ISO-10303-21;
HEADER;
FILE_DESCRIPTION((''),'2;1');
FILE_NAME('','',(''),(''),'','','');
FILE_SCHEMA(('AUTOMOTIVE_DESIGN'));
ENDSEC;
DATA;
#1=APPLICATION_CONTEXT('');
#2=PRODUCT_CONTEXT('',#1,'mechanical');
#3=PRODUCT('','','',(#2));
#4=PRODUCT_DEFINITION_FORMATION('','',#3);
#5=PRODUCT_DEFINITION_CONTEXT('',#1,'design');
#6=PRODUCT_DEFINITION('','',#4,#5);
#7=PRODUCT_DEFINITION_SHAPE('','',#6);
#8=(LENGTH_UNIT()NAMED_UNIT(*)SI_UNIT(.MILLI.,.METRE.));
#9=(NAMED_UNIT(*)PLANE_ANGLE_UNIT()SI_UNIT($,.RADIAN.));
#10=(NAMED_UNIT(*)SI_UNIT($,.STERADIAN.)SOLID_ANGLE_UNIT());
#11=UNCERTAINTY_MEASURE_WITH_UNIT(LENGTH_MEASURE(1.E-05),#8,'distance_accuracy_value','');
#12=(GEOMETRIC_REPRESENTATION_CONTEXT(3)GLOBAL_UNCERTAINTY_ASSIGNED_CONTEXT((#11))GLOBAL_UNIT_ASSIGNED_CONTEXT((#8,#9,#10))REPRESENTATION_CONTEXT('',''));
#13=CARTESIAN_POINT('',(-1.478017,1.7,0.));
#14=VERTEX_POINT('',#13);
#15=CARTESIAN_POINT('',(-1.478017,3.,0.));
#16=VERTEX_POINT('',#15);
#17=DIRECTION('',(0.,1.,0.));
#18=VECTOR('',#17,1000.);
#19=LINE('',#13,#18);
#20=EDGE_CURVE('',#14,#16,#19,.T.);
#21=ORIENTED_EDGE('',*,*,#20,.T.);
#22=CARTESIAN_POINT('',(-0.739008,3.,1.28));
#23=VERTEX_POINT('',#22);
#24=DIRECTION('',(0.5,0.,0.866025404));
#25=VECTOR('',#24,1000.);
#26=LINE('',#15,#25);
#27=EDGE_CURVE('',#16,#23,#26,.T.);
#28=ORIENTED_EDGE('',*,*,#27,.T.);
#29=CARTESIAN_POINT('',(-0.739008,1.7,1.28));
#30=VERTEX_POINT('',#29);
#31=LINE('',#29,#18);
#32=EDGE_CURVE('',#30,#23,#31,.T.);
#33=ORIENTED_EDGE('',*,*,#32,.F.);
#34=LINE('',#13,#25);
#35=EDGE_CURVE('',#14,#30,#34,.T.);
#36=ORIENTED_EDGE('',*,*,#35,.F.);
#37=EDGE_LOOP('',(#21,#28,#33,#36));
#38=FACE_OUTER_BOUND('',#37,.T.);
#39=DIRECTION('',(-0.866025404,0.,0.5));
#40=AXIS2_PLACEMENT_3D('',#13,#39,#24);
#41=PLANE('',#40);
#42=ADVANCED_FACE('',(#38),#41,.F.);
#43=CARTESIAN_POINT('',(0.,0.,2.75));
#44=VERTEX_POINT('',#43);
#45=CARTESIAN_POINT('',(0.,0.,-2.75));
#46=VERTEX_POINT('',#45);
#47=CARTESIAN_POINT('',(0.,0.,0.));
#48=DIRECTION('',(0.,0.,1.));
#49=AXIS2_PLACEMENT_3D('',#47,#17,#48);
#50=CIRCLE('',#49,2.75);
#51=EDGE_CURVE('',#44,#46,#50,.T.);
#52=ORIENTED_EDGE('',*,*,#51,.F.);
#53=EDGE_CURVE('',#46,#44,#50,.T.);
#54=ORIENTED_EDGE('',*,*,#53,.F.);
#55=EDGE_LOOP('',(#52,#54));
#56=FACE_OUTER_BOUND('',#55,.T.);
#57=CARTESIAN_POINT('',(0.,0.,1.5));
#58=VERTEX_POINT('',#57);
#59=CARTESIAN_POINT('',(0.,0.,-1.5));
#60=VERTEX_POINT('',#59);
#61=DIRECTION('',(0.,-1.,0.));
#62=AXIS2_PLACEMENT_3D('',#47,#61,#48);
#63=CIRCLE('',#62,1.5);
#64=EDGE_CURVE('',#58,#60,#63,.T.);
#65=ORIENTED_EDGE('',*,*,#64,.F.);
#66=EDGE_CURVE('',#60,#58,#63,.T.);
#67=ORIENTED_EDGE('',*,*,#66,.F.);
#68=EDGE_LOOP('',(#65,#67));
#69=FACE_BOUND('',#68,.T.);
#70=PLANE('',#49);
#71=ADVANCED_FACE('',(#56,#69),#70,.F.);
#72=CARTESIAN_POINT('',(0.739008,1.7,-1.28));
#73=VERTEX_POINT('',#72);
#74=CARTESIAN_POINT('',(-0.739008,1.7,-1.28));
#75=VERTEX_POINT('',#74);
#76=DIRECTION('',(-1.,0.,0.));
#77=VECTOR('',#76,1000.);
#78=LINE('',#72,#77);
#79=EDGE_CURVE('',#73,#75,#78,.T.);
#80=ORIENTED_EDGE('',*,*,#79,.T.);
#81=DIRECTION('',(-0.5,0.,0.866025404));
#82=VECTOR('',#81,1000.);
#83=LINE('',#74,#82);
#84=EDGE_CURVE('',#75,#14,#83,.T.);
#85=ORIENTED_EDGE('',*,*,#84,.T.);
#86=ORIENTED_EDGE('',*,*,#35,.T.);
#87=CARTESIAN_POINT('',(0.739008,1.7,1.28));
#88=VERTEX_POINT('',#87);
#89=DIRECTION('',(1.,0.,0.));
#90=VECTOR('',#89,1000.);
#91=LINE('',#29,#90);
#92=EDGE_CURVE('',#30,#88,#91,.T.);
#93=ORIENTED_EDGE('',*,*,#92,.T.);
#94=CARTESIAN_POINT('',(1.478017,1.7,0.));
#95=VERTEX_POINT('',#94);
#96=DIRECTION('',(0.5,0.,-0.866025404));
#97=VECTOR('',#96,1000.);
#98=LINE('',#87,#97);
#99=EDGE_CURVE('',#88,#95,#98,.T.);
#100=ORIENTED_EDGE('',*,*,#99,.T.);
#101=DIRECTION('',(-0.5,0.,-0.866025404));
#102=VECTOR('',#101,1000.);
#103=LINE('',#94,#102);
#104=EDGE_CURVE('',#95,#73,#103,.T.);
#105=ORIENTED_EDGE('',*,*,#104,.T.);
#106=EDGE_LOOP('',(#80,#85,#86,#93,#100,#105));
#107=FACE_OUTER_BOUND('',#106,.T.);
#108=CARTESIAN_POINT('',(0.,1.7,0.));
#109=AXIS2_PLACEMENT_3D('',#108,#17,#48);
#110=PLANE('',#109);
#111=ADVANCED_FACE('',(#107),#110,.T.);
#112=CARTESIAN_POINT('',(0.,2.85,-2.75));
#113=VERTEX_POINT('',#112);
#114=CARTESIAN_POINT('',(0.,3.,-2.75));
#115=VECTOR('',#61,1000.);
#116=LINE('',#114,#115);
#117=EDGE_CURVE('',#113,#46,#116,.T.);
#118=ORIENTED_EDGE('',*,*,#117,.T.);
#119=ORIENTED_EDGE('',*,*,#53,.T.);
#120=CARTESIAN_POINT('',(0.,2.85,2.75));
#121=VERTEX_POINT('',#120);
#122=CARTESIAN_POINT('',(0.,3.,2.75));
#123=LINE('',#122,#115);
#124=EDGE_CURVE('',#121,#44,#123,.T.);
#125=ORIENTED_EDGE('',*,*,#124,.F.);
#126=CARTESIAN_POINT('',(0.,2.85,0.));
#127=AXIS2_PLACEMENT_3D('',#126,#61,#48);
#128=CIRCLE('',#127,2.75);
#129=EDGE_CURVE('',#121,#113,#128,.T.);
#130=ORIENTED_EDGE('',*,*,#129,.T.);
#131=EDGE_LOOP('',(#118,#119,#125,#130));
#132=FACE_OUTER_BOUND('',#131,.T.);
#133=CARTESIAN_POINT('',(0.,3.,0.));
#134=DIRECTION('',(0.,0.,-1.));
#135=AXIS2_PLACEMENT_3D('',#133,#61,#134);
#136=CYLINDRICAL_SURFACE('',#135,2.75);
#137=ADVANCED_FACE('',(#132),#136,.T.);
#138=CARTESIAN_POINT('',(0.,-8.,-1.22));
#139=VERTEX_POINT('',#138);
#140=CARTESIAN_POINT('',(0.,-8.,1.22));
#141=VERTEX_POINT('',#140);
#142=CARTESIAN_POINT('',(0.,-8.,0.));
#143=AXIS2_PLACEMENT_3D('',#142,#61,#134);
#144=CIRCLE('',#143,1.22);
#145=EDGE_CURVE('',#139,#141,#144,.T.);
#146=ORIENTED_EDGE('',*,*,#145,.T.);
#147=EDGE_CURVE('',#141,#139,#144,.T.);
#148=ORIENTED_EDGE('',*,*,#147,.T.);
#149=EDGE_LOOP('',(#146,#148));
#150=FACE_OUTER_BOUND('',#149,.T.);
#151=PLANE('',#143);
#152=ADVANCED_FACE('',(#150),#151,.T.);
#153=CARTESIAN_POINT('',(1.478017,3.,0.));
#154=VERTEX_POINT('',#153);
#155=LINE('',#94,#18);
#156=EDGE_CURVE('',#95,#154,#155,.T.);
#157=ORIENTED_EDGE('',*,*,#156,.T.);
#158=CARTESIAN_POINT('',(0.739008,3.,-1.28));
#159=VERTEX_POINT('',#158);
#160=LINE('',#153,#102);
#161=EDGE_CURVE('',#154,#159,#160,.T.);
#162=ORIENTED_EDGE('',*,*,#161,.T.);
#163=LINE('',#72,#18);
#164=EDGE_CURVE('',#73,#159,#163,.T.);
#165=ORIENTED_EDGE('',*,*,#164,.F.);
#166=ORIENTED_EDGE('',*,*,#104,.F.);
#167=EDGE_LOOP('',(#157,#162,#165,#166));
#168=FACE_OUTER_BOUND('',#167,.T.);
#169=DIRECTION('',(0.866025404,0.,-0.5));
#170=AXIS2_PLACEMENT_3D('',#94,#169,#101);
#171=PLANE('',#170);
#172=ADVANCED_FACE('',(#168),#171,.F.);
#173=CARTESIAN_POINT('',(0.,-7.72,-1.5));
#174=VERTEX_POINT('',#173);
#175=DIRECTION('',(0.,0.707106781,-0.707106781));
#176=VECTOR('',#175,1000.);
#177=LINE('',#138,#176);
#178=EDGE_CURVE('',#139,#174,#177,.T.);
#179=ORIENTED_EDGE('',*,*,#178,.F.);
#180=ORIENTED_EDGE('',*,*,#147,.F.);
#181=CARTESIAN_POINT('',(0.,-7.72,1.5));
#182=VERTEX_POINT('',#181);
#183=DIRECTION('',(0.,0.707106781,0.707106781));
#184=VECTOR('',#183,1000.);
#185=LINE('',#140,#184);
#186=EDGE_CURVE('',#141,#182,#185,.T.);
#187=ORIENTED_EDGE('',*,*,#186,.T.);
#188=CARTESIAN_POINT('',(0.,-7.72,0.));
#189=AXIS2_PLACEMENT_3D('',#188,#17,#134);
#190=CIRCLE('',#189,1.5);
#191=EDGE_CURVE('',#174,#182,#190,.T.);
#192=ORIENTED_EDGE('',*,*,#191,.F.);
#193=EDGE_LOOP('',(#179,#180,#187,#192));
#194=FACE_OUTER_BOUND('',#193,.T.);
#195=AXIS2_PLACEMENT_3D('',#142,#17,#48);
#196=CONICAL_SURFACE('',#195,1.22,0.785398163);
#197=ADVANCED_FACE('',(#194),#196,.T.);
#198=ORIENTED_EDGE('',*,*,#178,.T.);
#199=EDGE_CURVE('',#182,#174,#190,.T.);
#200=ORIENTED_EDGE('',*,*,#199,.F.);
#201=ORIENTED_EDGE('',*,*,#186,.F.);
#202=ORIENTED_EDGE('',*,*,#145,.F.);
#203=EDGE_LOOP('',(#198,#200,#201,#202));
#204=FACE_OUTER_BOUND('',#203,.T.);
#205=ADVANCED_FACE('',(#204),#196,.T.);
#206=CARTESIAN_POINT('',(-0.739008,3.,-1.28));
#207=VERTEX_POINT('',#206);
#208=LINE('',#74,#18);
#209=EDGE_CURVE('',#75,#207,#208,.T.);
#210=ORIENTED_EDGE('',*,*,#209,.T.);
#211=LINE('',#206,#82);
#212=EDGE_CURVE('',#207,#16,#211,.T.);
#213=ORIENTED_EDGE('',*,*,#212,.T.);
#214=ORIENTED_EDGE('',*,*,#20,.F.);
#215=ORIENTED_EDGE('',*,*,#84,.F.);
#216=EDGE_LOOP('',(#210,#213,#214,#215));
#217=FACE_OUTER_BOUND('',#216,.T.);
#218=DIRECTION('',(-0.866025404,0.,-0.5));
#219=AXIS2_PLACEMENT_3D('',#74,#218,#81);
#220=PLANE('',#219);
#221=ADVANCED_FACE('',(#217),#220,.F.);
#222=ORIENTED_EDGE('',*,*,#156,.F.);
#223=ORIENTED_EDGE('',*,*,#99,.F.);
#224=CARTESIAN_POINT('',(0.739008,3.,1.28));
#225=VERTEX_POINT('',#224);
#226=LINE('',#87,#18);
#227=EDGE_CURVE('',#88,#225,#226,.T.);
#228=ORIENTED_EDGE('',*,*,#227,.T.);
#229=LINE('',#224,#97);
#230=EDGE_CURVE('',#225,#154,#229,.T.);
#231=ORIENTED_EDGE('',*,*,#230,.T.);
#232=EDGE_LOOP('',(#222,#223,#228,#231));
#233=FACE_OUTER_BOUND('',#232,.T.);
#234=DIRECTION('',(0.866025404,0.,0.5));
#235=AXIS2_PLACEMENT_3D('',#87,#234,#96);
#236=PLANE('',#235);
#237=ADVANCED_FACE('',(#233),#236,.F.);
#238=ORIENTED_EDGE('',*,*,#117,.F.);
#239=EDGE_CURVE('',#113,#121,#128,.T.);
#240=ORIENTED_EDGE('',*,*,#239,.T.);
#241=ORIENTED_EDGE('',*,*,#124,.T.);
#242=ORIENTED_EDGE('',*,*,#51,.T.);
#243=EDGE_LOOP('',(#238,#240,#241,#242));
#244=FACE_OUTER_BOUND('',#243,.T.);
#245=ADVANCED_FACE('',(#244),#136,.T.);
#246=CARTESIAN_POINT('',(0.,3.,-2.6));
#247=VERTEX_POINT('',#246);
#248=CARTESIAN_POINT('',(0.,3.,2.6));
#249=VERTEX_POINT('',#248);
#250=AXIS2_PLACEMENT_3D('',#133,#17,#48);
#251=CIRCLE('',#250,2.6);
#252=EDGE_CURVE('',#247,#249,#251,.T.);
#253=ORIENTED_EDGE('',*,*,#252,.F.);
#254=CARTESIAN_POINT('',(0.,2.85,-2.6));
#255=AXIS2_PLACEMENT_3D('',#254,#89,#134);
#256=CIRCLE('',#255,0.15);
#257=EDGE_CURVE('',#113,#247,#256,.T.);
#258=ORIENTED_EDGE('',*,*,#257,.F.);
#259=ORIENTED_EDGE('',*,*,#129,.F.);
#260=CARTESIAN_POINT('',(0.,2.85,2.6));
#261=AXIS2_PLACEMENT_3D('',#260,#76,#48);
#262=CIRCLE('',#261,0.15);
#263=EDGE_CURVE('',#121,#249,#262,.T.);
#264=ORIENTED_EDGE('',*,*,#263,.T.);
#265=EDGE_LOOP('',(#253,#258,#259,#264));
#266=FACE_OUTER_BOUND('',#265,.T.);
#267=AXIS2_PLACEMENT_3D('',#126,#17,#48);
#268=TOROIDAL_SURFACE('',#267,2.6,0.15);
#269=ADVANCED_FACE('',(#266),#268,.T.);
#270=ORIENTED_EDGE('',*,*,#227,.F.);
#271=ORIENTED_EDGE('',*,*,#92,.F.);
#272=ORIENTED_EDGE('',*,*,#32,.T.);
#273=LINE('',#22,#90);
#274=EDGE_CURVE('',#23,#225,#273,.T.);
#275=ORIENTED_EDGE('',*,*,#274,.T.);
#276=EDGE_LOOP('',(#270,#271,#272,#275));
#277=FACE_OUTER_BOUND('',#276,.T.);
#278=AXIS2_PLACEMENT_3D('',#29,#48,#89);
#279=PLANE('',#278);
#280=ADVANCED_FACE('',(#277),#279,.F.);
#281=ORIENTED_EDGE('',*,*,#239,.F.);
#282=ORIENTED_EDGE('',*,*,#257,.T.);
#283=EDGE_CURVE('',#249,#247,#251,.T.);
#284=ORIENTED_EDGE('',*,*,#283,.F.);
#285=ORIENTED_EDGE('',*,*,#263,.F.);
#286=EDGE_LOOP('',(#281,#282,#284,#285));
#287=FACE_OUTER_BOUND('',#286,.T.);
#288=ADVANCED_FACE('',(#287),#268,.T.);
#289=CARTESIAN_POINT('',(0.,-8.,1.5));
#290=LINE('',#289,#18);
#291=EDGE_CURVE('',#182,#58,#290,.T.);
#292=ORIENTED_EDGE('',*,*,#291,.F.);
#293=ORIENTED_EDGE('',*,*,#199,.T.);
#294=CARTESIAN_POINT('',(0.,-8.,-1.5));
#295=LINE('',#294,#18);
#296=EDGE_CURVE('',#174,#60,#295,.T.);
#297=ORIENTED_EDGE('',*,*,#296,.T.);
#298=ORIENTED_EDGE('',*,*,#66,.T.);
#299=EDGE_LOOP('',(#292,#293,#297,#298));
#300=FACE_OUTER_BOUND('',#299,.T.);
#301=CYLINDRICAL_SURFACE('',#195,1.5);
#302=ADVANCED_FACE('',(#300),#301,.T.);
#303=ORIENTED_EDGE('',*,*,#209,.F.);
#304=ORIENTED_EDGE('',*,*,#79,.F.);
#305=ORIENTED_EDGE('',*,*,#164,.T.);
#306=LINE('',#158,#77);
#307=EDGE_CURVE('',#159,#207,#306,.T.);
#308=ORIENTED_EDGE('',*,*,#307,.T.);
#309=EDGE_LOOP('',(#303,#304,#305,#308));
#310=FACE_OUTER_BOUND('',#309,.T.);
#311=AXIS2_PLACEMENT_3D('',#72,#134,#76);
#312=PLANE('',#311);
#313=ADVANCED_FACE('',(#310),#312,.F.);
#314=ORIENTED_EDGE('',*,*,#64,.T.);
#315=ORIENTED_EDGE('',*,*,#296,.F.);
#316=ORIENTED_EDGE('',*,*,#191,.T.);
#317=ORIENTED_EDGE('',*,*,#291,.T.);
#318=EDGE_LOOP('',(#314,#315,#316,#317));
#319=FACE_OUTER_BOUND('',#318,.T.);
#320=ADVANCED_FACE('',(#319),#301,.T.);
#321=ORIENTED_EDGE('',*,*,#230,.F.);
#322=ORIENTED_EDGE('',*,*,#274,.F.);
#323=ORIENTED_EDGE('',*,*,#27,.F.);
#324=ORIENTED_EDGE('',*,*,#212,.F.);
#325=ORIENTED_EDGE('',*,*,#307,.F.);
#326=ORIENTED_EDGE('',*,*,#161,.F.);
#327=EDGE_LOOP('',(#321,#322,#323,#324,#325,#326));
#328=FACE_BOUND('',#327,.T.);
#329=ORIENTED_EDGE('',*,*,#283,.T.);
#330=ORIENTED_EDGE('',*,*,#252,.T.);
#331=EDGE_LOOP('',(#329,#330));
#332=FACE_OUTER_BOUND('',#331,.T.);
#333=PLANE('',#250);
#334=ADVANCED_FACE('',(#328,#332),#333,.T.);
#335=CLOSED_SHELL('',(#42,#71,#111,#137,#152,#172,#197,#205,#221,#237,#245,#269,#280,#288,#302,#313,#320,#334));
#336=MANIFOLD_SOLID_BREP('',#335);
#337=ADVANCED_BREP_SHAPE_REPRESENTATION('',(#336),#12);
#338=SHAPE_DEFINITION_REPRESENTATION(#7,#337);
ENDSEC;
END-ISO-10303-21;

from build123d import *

# Parameters (mm, degrees)
SKETCH_1_R          = 2.75
EXTRUDE_1_DEPTH     = 3
CUT_EXTRUDE_1_DEPTH = 1.3
FILLET_1_R          = 0.15
SKETCH_5_R          = 1.5
EXTRUDE_2_DEPTH     = 8
CHAMFER_2_SIZE      = 0.28


with BuildPart() as part:
    # 草图1 → 凸台-拉伸1 (new body)
    with BuildSketch(Plane(origin=(0, 0, 0), x_dir=(1, 0, 0), z_dir=(0, 1, 0))):
        with Locations(Location((0, 0, 0), (0, 0, 270))):
            Circle(SKETCH_1_R)
    extrude(amount=EXTRUDE_1_DEPTH)

    # 草图2 → 切除-拉伸1 (cut)
    with BuildSketch(Plane(origin=(0, 3, 0), x_dir=(1, 0, 0), z_dir=(0, 1, 0))):
        Polygon((1.478016689, 0), (0.739008345, 1.28), (-0.739008345, 1.28), (-1.478016689, 0), (-0.739008345, -1.28), (0.739008345, -1.28), align=None)
    extrude(amount=-CUT_EXTRUDE_1_DEPTH, mode=Mode.SUBTRACT)

    # 圆角1
    fillet_1_edges = [part.edges().sort_by_distance(p)[0] for p in [
        (0, 3, -2.75),
    ]]
    fillet(fillet_1_edges, radius=FILLET_1_R)

    # 草图5 → 凸台-拉伸2 (add)
    with BuildSketch(Plane.XZ):
        with Locations(Location((0, 0, 0), (0, 0, 90))):
            Circle(SKETCH_5_R)
    extrude(amount=EXTRUDE_2_DEPTH)

    # 倒角2
    chamfer_2_edges = [part.edges().sort_by_distance(p)[0] for p in [
        (0, -8, -1.5),
    ]]
    chamfer(chamfer_2_edges, length=CHAMFER_2_SIZE)


solid = part.part
